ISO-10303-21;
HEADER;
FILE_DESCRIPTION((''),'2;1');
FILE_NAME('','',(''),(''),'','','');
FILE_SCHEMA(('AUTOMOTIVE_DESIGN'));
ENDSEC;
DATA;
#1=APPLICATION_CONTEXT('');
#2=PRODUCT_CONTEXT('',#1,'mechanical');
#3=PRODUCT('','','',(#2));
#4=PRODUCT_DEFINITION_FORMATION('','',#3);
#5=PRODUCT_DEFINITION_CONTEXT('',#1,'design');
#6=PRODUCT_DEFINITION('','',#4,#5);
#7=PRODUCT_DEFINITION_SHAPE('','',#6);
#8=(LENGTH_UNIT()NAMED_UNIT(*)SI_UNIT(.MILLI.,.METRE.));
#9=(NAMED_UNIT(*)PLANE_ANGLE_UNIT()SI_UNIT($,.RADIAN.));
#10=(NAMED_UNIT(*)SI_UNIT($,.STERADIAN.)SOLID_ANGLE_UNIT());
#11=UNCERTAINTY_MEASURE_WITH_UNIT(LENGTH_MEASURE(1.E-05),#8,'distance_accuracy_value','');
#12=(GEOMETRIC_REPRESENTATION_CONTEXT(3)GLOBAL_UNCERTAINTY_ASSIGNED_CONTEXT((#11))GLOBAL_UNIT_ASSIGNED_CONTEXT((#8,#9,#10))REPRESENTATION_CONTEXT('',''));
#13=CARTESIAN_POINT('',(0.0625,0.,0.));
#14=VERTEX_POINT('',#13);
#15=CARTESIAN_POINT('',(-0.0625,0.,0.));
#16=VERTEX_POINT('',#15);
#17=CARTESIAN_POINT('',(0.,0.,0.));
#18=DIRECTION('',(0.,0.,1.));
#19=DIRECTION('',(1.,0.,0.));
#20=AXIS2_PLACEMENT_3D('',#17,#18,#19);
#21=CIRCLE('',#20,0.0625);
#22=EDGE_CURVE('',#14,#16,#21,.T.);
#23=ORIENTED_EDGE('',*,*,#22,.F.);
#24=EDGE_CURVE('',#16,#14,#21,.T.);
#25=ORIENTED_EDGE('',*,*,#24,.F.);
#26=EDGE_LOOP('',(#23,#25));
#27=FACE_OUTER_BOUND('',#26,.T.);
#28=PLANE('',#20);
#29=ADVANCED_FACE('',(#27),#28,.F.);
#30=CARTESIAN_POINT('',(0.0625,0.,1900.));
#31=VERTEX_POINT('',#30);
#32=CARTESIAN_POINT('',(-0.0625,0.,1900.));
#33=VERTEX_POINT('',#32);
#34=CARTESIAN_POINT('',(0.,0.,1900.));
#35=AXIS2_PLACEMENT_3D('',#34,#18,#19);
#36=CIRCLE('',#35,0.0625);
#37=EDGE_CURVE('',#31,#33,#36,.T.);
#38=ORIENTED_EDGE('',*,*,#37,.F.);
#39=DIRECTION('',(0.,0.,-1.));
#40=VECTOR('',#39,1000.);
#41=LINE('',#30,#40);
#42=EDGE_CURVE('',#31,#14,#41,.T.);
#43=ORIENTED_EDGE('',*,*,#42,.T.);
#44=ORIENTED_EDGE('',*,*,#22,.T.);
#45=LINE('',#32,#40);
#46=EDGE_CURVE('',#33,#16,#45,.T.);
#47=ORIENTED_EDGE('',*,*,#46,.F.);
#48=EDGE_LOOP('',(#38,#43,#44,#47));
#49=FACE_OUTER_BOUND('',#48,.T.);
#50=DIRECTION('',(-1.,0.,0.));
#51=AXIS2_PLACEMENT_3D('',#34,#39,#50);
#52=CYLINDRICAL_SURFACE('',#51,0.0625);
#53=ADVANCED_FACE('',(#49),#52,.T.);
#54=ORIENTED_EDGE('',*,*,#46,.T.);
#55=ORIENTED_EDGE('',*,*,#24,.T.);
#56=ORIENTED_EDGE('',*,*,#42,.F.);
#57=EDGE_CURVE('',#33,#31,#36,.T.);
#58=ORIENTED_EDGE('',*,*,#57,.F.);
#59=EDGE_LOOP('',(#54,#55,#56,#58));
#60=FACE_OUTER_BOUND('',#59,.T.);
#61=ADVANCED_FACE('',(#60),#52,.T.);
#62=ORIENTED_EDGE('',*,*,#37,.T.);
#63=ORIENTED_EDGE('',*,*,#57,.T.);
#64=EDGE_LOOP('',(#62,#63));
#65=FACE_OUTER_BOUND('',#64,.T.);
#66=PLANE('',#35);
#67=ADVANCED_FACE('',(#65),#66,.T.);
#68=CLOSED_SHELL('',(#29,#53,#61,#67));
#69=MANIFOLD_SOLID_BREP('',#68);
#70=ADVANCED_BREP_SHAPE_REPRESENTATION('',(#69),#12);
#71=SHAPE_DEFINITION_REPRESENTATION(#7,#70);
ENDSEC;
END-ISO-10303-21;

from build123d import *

# Parameters (mm, degrees)
SKETCH1_R           = 0.0625
BOSS_EXTRUDE1_DEPTH = 1900


with BuildPart() as part:
    # Sketch1 → Boss-Extrude1 (new body)
    with BuildSketch(Plane.XY):
        Circle(SKETCH1_R)
    extrude(amount=BOSS_EXTRUDE1_DEPTH)


solid = part.part
